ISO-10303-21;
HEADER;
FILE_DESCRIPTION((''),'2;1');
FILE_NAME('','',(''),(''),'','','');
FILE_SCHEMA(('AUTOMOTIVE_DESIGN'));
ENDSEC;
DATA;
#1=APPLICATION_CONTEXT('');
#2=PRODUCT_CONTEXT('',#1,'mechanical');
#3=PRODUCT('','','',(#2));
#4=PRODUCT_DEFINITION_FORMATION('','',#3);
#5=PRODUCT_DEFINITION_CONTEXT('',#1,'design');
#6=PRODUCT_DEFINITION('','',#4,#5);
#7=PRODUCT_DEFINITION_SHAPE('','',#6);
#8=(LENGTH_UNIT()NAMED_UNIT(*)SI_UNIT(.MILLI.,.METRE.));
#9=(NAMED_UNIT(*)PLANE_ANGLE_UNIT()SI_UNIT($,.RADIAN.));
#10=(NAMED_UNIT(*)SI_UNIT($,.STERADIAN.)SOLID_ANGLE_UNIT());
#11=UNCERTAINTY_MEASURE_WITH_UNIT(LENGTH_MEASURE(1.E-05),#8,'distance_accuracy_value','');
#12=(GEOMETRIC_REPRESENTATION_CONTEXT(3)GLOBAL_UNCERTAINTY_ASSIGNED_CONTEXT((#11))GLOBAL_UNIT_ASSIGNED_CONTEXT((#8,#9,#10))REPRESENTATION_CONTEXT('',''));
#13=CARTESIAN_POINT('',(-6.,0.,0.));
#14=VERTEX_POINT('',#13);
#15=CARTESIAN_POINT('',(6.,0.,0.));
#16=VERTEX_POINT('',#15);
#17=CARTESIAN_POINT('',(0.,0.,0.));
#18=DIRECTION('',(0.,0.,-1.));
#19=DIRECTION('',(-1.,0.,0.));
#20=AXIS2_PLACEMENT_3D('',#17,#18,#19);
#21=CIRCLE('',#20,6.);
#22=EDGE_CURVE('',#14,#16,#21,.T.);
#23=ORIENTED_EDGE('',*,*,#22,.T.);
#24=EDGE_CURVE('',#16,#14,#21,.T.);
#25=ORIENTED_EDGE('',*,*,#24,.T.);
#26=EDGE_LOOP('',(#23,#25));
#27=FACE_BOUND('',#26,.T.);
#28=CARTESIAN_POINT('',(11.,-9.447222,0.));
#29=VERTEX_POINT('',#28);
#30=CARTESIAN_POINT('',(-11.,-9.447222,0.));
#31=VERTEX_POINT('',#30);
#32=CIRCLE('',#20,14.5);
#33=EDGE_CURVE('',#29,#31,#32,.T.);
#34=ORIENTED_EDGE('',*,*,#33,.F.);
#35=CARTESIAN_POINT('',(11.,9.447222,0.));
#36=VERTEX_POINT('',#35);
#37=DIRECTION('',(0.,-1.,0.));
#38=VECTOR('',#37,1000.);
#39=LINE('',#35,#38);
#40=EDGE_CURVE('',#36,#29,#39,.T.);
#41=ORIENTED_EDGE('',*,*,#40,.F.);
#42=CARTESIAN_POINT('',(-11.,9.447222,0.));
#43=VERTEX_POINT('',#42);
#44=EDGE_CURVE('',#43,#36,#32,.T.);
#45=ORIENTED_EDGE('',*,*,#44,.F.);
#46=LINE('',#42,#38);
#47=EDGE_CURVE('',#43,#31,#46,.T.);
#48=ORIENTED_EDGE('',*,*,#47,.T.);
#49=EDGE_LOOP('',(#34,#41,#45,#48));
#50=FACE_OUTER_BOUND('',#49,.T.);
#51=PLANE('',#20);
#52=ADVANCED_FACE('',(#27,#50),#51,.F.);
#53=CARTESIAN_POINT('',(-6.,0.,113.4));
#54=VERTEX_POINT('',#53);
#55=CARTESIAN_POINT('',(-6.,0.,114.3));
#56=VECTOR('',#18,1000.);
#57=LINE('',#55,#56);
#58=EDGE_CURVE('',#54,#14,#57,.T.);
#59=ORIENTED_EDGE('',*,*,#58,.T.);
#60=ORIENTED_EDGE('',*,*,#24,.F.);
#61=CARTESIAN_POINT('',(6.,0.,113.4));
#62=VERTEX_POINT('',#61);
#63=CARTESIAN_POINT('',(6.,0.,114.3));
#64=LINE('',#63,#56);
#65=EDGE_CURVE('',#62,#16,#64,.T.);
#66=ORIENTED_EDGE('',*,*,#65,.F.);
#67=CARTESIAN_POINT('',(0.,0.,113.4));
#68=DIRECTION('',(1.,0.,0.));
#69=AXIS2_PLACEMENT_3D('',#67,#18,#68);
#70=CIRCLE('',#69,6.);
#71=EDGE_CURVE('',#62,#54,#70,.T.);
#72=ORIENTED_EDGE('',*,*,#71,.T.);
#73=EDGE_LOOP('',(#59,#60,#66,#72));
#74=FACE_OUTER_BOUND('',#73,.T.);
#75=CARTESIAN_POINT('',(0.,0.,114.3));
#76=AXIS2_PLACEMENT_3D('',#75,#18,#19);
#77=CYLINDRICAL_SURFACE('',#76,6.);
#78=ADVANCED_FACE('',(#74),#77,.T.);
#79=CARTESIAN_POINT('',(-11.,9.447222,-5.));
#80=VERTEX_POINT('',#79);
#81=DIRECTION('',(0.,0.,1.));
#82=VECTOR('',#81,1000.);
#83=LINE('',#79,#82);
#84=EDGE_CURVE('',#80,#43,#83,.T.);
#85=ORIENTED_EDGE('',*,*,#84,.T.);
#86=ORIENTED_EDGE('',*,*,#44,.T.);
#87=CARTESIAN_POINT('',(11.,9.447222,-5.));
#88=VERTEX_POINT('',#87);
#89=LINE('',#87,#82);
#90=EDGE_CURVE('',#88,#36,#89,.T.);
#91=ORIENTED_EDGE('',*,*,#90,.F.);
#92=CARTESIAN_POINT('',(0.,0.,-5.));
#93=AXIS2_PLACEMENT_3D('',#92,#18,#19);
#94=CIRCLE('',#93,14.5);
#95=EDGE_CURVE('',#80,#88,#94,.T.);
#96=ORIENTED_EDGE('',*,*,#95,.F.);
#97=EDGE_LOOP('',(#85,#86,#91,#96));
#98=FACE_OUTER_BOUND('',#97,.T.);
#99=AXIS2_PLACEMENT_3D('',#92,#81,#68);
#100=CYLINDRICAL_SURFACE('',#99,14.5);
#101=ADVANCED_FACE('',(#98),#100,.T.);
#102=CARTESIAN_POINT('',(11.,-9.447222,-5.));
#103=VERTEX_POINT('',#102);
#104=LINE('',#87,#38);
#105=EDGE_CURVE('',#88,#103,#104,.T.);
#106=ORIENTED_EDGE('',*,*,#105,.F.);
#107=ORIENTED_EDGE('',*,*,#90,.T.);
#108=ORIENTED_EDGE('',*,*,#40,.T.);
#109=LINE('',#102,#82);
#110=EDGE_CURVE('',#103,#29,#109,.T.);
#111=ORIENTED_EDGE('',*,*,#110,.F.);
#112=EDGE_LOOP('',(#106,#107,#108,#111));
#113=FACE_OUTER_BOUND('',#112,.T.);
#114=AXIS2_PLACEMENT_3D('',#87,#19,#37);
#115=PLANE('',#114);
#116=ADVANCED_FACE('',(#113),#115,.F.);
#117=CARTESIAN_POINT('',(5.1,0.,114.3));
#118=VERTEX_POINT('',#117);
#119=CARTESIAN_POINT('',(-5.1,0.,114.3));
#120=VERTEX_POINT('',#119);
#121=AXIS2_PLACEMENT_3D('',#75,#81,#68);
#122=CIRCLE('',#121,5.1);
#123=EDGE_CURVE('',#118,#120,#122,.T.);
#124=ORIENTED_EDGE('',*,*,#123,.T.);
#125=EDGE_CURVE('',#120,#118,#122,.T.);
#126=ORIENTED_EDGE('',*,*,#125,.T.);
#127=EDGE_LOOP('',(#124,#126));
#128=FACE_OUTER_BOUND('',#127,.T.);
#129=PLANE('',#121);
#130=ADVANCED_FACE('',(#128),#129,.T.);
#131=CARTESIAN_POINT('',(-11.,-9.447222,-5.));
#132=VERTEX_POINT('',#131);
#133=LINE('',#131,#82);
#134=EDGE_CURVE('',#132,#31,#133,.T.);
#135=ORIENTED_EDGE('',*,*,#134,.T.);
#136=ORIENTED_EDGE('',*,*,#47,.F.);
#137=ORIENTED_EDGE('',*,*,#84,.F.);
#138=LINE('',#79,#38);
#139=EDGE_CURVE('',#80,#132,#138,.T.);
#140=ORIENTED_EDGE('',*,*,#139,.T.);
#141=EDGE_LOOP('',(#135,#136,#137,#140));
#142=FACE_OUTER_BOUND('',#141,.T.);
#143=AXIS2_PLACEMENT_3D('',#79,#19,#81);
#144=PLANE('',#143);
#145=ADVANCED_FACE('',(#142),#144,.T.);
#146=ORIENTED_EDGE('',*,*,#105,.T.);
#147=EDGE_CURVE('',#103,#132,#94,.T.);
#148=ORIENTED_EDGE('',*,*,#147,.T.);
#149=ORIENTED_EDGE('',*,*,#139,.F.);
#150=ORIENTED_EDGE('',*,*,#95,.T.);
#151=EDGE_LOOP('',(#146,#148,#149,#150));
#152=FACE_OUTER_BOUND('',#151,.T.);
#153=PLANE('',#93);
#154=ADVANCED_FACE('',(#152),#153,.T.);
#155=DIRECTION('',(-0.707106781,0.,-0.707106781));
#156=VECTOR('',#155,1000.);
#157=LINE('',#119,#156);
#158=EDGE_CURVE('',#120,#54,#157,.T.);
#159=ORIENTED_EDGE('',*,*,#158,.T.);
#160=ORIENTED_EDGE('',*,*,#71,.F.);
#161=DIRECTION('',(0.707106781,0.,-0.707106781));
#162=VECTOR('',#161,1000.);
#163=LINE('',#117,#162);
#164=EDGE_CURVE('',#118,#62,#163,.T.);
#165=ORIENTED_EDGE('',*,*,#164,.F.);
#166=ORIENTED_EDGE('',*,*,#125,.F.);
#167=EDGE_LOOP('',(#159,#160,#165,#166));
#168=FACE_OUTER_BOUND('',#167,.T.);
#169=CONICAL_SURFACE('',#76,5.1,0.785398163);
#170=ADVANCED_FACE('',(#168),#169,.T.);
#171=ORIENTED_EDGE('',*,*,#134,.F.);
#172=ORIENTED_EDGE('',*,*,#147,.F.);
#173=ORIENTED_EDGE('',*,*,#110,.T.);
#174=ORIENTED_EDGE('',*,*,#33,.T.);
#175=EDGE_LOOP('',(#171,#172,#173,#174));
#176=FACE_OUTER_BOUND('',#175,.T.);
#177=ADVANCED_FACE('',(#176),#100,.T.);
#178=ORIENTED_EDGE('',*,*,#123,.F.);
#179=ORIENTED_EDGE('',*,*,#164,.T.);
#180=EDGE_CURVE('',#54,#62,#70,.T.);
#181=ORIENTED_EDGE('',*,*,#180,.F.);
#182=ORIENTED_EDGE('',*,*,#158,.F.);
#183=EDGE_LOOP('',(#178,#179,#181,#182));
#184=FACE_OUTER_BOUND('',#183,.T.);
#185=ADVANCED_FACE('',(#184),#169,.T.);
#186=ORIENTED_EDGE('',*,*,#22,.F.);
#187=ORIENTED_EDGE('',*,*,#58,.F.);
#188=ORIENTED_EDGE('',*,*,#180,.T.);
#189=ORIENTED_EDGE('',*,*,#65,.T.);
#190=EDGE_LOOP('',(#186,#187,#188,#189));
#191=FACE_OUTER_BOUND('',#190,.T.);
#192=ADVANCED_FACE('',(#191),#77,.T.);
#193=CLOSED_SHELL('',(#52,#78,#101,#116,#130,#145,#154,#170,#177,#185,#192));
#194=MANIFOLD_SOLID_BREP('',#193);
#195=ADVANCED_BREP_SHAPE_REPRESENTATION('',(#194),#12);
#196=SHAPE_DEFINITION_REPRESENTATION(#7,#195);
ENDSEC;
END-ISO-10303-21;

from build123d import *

# Parameters (mm, degrees)
SKETCH1_R           = 6
BOSS_EXTRUDE1_DEPTH = 114.3
CHAMFER2_SIZE       = 0.9
BOSS_EXTRUDE2_DEPTH = 5


with BuildPart() as part:
    # Sketch1 → Boss-Extrude1 (new body)
    with BuildSketch(Plane.XY):
        Circle(SKETCH1_R)
    extrude(amount=BOSS_EXTRUDE1_DEPTH)

    # Chamfer2
    chamfer2_edges = [part.edges().sort_by_distance(p)[0] for p in [
        (-6, 0, 114.3),
    ]]
    chamfer(chamfer2_edges, length=CHAMFER2_SIZE)

    # Sketch2 → Boss-Extrude2 (add)
    with BuildSketch(Plane(origin=(0, 0, 0), x_dir=(-1, 0, 0), z_dir=(0, 0, -1))):
        with BuildLine():
            Line((11, 9.447221814), (11, -9.447221814))
            ThreePointArc((11, -9.447221814), (0, -14.5), (-11, -9.447221814))
            Line((-11, -9.447221814), (-11, 9.447221814))
            ThreePointArc((-11, 9.447221814), (0, 14.5), (11, 9.447221814))
        make_face()
    extrude(amount=BOSS_EXTRUDE2_DEPTH)


solid = part.part
